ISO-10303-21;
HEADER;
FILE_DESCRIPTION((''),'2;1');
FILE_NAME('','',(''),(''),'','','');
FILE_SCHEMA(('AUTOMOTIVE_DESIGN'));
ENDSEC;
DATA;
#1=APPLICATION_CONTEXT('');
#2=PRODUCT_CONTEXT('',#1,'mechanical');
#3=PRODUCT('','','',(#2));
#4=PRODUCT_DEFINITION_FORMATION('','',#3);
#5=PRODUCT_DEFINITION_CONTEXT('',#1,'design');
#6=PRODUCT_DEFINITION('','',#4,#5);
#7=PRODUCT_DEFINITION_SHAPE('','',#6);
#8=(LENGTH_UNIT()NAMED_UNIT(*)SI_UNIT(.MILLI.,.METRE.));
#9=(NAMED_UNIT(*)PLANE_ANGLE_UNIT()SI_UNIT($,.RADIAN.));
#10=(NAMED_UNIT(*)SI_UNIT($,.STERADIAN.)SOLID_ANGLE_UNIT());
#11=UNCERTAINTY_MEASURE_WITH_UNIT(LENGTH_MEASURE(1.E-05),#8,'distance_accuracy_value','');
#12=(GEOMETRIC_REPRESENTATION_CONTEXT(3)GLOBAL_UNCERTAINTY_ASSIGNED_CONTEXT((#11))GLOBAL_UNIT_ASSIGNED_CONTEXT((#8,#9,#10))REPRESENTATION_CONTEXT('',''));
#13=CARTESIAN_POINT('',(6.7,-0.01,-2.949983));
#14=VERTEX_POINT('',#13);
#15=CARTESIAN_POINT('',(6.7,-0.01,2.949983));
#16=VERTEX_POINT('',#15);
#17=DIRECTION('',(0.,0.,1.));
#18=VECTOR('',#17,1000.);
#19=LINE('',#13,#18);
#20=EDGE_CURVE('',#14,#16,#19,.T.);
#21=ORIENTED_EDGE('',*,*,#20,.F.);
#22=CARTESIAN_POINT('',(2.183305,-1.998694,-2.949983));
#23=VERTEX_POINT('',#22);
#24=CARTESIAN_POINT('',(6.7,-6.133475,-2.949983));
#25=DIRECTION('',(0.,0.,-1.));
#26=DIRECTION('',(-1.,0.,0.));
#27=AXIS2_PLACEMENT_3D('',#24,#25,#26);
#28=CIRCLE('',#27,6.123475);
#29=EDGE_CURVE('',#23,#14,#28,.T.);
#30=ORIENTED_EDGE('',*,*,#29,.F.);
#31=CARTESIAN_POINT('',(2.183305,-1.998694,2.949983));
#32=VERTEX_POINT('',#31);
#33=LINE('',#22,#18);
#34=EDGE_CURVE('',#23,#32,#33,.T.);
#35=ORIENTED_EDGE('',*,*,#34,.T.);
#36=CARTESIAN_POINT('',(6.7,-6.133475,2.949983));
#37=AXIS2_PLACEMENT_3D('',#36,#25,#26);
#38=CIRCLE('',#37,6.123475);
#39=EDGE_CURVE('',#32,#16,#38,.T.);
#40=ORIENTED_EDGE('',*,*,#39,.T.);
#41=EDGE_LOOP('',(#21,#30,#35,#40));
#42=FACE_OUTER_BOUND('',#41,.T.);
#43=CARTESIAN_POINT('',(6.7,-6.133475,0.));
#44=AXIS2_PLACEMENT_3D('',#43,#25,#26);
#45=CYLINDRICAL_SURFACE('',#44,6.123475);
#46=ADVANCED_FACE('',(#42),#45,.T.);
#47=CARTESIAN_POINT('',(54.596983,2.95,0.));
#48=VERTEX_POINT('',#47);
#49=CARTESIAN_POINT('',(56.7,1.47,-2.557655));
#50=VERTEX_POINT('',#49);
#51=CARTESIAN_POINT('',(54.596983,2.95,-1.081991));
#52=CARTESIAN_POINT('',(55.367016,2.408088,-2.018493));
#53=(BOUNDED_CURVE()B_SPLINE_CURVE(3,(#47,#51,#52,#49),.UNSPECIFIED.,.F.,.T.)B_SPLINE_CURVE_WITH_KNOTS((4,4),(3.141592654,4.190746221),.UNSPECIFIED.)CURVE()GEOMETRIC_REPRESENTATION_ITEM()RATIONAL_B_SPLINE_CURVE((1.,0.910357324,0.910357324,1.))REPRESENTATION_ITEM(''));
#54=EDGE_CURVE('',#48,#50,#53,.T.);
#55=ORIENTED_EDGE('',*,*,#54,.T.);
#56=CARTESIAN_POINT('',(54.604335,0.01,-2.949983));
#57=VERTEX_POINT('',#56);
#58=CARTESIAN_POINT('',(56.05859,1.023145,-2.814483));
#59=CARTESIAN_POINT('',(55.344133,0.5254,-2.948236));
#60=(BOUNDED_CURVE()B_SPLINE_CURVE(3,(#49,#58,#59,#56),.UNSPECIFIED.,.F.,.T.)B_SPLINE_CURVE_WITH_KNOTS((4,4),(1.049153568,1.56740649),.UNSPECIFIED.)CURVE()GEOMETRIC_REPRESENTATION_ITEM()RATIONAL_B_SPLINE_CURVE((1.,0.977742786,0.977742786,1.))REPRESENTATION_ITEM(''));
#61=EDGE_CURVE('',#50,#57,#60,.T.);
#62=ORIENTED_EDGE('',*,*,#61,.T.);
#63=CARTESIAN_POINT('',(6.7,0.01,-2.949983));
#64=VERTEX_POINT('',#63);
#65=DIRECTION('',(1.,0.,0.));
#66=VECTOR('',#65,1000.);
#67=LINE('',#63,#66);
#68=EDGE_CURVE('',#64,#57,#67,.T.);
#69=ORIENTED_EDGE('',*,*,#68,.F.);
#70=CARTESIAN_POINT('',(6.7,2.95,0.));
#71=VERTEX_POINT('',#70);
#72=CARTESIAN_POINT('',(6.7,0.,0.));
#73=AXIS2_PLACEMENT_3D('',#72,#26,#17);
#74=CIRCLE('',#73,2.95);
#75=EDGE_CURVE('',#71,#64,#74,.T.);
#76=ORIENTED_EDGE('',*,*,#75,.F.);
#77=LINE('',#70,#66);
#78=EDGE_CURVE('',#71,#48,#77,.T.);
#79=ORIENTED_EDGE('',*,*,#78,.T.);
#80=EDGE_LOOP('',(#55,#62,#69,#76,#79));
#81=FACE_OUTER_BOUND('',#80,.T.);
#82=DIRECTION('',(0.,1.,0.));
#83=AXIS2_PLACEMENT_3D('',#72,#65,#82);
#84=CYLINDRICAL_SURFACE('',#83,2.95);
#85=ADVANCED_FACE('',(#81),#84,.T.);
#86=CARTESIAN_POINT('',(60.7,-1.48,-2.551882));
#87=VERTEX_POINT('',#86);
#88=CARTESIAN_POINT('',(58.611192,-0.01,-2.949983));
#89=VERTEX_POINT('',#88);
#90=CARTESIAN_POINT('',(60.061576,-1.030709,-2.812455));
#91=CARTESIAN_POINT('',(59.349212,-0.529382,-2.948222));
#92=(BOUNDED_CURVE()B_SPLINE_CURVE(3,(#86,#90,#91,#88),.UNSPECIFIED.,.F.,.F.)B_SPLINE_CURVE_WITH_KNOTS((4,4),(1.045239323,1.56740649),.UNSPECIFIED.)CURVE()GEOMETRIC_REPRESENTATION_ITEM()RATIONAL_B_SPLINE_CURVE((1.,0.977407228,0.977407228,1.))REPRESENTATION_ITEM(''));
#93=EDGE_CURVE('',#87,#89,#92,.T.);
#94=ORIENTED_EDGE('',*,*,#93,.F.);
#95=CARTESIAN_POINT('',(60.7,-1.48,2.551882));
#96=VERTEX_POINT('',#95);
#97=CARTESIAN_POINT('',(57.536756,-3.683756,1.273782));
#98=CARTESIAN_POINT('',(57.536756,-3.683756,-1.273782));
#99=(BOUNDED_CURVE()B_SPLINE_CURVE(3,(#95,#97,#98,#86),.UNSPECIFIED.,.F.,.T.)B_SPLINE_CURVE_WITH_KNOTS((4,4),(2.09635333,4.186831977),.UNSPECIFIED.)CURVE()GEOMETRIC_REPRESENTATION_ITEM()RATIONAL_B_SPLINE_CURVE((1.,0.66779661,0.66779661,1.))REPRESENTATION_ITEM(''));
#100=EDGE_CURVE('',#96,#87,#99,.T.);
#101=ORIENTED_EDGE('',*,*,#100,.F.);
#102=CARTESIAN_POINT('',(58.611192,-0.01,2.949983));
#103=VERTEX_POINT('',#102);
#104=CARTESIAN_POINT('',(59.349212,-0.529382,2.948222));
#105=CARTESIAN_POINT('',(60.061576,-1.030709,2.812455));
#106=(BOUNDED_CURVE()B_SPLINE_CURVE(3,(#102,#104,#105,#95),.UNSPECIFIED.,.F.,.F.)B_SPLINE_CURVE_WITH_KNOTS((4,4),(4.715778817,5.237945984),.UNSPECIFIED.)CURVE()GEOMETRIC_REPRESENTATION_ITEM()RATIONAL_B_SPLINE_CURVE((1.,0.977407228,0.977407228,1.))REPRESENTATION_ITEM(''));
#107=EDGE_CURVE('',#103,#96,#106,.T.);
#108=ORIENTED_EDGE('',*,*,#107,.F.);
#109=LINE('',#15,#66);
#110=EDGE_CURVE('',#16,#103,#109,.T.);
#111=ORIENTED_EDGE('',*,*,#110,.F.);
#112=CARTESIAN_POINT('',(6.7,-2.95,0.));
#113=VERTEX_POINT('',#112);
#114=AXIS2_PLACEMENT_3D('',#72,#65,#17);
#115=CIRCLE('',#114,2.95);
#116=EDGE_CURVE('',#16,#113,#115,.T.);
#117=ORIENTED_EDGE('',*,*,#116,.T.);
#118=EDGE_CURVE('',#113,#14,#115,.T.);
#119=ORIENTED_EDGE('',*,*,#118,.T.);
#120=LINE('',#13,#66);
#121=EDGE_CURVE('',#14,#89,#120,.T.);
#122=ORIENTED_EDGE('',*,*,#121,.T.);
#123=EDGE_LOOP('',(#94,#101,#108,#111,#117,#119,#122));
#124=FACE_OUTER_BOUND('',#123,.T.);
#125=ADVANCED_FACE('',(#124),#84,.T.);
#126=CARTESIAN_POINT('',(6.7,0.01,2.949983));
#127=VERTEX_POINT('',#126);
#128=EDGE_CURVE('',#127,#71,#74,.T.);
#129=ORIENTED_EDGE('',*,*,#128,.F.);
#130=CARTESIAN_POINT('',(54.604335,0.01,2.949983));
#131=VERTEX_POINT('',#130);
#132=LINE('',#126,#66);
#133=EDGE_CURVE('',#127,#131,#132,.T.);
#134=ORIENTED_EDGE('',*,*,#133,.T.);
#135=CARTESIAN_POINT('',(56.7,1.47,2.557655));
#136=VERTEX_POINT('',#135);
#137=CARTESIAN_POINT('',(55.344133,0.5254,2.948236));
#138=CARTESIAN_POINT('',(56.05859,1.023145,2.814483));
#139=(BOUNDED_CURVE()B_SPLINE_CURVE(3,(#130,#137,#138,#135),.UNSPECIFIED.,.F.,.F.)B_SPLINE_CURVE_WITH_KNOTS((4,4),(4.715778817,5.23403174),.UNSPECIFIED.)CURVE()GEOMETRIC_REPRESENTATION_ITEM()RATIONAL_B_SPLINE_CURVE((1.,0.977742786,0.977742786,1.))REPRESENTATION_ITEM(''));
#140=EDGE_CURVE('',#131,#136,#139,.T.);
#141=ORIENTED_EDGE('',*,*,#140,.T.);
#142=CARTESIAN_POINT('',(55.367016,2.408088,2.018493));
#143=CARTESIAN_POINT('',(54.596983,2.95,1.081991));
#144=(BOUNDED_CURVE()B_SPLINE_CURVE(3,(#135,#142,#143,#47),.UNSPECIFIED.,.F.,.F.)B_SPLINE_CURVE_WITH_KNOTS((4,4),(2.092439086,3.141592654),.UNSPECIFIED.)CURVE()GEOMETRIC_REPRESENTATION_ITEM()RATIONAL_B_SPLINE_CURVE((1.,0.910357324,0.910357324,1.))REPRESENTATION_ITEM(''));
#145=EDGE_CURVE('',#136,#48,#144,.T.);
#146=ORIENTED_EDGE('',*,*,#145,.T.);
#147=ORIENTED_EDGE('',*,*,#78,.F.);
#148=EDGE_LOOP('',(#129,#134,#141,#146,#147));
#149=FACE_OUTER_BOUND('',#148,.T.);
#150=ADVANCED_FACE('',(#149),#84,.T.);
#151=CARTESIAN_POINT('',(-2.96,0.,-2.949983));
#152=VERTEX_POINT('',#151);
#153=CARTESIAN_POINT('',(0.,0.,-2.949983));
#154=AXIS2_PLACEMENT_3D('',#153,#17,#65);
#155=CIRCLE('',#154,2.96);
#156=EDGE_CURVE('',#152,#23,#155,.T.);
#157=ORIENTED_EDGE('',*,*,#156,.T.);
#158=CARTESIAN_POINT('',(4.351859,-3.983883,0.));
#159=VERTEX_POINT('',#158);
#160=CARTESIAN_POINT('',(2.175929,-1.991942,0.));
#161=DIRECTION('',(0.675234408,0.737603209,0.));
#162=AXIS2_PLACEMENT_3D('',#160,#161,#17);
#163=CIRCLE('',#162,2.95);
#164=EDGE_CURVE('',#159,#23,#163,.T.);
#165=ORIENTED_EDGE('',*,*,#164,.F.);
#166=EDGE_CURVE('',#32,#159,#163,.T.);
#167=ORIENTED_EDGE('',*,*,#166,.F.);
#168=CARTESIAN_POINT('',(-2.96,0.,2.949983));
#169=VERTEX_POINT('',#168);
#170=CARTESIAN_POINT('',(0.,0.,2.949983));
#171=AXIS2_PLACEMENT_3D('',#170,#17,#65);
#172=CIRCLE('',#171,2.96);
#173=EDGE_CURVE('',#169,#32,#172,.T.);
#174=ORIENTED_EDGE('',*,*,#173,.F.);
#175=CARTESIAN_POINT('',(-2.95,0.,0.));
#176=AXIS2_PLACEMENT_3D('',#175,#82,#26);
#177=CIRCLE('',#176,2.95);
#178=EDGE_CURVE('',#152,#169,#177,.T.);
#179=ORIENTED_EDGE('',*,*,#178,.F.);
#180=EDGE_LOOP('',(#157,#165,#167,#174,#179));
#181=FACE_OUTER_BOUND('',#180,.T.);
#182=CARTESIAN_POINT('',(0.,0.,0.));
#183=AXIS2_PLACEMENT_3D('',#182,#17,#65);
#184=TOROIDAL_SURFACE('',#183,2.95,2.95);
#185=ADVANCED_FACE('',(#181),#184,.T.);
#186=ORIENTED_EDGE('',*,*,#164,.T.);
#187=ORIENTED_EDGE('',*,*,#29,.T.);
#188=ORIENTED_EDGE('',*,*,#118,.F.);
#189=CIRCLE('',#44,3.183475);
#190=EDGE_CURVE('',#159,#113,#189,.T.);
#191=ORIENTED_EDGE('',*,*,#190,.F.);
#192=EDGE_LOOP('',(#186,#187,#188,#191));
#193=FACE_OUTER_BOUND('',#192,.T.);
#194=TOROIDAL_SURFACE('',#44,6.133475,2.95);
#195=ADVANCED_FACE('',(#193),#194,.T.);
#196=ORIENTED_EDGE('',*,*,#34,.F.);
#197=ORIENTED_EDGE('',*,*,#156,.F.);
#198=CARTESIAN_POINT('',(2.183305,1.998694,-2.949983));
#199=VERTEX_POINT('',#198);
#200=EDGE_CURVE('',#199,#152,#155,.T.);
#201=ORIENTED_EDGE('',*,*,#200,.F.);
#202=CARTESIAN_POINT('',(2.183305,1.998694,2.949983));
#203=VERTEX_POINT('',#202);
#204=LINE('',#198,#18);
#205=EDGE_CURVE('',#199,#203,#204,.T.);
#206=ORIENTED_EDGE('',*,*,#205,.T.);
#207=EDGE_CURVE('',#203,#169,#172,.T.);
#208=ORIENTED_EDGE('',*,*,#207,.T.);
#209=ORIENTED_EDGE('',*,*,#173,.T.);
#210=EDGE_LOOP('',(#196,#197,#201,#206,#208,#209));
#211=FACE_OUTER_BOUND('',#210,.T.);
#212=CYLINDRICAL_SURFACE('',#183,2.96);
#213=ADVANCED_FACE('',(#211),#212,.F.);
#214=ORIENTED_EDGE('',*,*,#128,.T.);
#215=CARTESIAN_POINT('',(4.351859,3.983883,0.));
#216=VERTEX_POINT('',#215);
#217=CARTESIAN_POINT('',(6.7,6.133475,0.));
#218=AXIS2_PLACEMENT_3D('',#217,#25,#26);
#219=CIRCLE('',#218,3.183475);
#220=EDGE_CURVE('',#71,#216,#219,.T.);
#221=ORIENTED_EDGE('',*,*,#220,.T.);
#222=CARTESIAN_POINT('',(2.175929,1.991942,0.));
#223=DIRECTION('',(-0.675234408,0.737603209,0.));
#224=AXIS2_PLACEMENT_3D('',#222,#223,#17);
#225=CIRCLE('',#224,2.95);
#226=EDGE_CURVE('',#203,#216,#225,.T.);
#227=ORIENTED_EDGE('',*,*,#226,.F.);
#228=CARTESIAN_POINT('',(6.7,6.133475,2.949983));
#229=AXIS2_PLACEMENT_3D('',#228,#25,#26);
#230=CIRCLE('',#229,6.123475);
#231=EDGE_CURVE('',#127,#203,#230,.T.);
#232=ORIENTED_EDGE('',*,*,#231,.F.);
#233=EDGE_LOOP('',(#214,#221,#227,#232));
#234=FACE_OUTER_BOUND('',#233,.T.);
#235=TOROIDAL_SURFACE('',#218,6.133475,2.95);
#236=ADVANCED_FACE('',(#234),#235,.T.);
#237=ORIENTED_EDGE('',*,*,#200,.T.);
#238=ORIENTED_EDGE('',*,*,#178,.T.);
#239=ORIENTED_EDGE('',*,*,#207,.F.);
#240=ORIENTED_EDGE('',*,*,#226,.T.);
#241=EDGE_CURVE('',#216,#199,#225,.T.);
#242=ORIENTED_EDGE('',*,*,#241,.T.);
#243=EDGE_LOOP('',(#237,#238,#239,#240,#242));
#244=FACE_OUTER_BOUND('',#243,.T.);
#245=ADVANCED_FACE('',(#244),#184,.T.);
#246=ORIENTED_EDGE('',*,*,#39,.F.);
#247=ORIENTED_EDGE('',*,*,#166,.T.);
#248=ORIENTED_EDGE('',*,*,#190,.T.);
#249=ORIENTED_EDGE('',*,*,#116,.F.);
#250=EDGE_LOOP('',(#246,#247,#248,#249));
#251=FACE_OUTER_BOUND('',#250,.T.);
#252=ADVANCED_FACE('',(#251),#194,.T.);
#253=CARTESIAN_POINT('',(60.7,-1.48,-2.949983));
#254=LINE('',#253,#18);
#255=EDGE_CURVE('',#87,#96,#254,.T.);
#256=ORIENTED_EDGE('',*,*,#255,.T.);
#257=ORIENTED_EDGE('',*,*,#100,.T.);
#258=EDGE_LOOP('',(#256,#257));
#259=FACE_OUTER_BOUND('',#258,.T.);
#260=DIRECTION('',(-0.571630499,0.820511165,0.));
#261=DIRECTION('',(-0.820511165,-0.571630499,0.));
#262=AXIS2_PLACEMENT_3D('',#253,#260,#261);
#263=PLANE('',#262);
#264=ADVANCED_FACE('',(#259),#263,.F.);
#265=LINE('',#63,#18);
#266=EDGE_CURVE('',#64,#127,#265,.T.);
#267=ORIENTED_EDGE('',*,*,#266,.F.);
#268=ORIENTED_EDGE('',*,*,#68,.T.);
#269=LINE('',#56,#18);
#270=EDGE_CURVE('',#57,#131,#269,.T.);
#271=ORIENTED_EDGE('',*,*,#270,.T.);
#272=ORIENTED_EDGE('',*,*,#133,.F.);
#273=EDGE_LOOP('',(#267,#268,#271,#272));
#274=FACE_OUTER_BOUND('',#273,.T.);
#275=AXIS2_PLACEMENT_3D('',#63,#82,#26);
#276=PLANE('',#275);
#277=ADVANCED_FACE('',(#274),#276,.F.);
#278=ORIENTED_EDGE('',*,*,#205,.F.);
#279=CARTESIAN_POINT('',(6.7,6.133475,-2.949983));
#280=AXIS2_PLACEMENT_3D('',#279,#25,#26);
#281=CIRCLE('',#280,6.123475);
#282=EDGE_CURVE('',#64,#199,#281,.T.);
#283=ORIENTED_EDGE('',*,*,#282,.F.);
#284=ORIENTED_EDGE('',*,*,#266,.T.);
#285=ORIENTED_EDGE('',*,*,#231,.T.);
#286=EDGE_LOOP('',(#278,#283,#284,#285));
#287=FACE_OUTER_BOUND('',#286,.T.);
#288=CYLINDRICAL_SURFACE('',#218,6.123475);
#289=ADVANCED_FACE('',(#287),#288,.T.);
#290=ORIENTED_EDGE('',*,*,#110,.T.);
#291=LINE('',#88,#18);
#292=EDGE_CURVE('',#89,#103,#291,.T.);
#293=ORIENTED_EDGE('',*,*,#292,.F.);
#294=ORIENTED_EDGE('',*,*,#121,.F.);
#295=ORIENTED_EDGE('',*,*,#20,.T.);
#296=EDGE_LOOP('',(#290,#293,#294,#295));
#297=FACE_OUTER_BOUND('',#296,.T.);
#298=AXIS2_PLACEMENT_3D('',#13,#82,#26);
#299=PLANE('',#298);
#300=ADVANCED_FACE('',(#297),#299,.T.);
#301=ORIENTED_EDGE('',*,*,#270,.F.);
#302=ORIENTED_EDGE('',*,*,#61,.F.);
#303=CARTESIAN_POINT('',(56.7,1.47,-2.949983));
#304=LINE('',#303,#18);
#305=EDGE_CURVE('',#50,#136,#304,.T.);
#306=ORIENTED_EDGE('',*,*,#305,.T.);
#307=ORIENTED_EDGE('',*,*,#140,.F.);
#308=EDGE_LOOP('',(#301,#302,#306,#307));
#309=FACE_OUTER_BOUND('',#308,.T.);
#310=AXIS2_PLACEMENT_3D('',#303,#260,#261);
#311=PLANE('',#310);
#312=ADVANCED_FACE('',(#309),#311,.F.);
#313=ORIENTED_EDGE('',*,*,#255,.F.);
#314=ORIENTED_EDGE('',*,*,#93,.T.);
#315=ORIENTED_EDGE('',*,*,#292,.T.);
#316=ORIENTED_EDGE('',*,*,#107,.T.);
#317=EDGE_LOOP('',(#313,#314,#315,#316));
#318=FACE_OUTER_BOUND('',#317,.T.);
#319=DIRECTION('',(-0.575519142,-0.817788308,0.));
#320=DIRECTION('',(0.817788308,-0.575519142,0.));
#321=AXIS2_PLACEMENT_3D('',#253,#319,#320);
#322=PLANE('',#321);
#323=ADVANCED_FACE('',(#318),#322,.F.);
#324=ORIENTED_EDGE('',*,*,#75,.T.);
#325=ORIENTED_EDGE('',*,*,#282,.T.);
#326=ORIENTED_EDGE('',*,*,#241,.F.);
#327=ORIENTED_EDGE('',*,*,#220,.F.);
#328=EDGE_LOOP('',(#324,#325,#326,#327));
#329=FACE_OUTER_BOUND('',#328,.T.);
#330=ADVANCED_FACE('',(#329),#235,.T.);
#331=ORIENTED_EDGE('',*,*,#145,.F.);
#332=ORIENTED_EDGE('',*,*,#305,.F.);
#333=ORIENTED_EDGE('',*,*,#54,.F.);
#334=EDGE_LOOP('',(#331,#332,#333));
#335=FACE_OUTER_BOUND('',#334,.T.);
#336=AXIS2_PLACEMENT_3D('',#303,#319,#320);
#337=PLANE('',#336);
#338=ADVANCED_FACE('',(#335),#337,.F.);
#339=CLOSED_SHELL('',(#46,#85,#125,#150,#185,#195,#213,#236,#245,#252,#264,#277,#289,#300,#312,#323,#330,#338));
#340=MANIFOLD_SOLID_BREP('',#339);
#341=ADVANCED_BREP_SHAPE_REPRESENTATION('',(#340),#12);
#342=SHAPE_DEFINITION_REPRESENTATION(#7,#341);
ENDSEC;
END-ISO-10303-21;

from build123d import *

# Parameters (mm, degrees)
CUT_EXTRUDE1_DEPTH      = 62.057369758
CUT_EXTRUDE1_DEPTH_BACK = 62.057369758


with BuildPart() as part:
    # Sweep2: sweep along a path in Dimension sketch
    with BuildLine(Plane.XY) as sweep2_path:
        Line((56.7, 2.95), (6.7, 2.95))
        ThreePointArc((6.7, 2.95), (5.417163248, 3.21991314), (4.351858935, 3.983883006))
        ThreePointArc((4.351858935, 3.983883006), (-5.9, 0), (4.351858935, -3.983883006))
        ThreePointArc((4.351858935, -3.983883006), (5.417163248, -3.21991314), (6.7, -2.95))
        Line((6.7, -2.95), (60.7, -2.95))
    # Sketch2 → Sweep2 (sweep)
    with BuildSketch(Plane(origin=(56.7, 2.95, 0), x_dir=(0, 0, 1), z_dir=(-1, 0, 0))):
        with BuildLine():
            Line((-2.949983051, -2.94), (2.949983051, -2.94))
            ThreePointArc((2.949983051, -2.94), (0, 0), (-2.949983051, -2.94))
        make_face()
    sweep(path=sweep2_path.line)

    # Sketch3 → Cut-Extrude1 (cut, two sides: drawn at the far end of the back side and taken through both)
    with BuildSketch(Plane.XY.offset(-CUT_EXTRUDE1_DEPTH_BACK)):
        Polygon((56.7, 1.47), (54.596982728, 2.95), (60.71, 2.95), (60.71, -2.95), (58.589980652, -2.95), (60.7, -1.48), (58.596982728, 0), (54.589980652, 0), align=None)
    extrude(amount=CUT_EXTRUDE1_DEPTH + CUT_EXTRUDE1_DEPTH_BACK, mode=Mode.SUBTRACT)


solid = part.part
